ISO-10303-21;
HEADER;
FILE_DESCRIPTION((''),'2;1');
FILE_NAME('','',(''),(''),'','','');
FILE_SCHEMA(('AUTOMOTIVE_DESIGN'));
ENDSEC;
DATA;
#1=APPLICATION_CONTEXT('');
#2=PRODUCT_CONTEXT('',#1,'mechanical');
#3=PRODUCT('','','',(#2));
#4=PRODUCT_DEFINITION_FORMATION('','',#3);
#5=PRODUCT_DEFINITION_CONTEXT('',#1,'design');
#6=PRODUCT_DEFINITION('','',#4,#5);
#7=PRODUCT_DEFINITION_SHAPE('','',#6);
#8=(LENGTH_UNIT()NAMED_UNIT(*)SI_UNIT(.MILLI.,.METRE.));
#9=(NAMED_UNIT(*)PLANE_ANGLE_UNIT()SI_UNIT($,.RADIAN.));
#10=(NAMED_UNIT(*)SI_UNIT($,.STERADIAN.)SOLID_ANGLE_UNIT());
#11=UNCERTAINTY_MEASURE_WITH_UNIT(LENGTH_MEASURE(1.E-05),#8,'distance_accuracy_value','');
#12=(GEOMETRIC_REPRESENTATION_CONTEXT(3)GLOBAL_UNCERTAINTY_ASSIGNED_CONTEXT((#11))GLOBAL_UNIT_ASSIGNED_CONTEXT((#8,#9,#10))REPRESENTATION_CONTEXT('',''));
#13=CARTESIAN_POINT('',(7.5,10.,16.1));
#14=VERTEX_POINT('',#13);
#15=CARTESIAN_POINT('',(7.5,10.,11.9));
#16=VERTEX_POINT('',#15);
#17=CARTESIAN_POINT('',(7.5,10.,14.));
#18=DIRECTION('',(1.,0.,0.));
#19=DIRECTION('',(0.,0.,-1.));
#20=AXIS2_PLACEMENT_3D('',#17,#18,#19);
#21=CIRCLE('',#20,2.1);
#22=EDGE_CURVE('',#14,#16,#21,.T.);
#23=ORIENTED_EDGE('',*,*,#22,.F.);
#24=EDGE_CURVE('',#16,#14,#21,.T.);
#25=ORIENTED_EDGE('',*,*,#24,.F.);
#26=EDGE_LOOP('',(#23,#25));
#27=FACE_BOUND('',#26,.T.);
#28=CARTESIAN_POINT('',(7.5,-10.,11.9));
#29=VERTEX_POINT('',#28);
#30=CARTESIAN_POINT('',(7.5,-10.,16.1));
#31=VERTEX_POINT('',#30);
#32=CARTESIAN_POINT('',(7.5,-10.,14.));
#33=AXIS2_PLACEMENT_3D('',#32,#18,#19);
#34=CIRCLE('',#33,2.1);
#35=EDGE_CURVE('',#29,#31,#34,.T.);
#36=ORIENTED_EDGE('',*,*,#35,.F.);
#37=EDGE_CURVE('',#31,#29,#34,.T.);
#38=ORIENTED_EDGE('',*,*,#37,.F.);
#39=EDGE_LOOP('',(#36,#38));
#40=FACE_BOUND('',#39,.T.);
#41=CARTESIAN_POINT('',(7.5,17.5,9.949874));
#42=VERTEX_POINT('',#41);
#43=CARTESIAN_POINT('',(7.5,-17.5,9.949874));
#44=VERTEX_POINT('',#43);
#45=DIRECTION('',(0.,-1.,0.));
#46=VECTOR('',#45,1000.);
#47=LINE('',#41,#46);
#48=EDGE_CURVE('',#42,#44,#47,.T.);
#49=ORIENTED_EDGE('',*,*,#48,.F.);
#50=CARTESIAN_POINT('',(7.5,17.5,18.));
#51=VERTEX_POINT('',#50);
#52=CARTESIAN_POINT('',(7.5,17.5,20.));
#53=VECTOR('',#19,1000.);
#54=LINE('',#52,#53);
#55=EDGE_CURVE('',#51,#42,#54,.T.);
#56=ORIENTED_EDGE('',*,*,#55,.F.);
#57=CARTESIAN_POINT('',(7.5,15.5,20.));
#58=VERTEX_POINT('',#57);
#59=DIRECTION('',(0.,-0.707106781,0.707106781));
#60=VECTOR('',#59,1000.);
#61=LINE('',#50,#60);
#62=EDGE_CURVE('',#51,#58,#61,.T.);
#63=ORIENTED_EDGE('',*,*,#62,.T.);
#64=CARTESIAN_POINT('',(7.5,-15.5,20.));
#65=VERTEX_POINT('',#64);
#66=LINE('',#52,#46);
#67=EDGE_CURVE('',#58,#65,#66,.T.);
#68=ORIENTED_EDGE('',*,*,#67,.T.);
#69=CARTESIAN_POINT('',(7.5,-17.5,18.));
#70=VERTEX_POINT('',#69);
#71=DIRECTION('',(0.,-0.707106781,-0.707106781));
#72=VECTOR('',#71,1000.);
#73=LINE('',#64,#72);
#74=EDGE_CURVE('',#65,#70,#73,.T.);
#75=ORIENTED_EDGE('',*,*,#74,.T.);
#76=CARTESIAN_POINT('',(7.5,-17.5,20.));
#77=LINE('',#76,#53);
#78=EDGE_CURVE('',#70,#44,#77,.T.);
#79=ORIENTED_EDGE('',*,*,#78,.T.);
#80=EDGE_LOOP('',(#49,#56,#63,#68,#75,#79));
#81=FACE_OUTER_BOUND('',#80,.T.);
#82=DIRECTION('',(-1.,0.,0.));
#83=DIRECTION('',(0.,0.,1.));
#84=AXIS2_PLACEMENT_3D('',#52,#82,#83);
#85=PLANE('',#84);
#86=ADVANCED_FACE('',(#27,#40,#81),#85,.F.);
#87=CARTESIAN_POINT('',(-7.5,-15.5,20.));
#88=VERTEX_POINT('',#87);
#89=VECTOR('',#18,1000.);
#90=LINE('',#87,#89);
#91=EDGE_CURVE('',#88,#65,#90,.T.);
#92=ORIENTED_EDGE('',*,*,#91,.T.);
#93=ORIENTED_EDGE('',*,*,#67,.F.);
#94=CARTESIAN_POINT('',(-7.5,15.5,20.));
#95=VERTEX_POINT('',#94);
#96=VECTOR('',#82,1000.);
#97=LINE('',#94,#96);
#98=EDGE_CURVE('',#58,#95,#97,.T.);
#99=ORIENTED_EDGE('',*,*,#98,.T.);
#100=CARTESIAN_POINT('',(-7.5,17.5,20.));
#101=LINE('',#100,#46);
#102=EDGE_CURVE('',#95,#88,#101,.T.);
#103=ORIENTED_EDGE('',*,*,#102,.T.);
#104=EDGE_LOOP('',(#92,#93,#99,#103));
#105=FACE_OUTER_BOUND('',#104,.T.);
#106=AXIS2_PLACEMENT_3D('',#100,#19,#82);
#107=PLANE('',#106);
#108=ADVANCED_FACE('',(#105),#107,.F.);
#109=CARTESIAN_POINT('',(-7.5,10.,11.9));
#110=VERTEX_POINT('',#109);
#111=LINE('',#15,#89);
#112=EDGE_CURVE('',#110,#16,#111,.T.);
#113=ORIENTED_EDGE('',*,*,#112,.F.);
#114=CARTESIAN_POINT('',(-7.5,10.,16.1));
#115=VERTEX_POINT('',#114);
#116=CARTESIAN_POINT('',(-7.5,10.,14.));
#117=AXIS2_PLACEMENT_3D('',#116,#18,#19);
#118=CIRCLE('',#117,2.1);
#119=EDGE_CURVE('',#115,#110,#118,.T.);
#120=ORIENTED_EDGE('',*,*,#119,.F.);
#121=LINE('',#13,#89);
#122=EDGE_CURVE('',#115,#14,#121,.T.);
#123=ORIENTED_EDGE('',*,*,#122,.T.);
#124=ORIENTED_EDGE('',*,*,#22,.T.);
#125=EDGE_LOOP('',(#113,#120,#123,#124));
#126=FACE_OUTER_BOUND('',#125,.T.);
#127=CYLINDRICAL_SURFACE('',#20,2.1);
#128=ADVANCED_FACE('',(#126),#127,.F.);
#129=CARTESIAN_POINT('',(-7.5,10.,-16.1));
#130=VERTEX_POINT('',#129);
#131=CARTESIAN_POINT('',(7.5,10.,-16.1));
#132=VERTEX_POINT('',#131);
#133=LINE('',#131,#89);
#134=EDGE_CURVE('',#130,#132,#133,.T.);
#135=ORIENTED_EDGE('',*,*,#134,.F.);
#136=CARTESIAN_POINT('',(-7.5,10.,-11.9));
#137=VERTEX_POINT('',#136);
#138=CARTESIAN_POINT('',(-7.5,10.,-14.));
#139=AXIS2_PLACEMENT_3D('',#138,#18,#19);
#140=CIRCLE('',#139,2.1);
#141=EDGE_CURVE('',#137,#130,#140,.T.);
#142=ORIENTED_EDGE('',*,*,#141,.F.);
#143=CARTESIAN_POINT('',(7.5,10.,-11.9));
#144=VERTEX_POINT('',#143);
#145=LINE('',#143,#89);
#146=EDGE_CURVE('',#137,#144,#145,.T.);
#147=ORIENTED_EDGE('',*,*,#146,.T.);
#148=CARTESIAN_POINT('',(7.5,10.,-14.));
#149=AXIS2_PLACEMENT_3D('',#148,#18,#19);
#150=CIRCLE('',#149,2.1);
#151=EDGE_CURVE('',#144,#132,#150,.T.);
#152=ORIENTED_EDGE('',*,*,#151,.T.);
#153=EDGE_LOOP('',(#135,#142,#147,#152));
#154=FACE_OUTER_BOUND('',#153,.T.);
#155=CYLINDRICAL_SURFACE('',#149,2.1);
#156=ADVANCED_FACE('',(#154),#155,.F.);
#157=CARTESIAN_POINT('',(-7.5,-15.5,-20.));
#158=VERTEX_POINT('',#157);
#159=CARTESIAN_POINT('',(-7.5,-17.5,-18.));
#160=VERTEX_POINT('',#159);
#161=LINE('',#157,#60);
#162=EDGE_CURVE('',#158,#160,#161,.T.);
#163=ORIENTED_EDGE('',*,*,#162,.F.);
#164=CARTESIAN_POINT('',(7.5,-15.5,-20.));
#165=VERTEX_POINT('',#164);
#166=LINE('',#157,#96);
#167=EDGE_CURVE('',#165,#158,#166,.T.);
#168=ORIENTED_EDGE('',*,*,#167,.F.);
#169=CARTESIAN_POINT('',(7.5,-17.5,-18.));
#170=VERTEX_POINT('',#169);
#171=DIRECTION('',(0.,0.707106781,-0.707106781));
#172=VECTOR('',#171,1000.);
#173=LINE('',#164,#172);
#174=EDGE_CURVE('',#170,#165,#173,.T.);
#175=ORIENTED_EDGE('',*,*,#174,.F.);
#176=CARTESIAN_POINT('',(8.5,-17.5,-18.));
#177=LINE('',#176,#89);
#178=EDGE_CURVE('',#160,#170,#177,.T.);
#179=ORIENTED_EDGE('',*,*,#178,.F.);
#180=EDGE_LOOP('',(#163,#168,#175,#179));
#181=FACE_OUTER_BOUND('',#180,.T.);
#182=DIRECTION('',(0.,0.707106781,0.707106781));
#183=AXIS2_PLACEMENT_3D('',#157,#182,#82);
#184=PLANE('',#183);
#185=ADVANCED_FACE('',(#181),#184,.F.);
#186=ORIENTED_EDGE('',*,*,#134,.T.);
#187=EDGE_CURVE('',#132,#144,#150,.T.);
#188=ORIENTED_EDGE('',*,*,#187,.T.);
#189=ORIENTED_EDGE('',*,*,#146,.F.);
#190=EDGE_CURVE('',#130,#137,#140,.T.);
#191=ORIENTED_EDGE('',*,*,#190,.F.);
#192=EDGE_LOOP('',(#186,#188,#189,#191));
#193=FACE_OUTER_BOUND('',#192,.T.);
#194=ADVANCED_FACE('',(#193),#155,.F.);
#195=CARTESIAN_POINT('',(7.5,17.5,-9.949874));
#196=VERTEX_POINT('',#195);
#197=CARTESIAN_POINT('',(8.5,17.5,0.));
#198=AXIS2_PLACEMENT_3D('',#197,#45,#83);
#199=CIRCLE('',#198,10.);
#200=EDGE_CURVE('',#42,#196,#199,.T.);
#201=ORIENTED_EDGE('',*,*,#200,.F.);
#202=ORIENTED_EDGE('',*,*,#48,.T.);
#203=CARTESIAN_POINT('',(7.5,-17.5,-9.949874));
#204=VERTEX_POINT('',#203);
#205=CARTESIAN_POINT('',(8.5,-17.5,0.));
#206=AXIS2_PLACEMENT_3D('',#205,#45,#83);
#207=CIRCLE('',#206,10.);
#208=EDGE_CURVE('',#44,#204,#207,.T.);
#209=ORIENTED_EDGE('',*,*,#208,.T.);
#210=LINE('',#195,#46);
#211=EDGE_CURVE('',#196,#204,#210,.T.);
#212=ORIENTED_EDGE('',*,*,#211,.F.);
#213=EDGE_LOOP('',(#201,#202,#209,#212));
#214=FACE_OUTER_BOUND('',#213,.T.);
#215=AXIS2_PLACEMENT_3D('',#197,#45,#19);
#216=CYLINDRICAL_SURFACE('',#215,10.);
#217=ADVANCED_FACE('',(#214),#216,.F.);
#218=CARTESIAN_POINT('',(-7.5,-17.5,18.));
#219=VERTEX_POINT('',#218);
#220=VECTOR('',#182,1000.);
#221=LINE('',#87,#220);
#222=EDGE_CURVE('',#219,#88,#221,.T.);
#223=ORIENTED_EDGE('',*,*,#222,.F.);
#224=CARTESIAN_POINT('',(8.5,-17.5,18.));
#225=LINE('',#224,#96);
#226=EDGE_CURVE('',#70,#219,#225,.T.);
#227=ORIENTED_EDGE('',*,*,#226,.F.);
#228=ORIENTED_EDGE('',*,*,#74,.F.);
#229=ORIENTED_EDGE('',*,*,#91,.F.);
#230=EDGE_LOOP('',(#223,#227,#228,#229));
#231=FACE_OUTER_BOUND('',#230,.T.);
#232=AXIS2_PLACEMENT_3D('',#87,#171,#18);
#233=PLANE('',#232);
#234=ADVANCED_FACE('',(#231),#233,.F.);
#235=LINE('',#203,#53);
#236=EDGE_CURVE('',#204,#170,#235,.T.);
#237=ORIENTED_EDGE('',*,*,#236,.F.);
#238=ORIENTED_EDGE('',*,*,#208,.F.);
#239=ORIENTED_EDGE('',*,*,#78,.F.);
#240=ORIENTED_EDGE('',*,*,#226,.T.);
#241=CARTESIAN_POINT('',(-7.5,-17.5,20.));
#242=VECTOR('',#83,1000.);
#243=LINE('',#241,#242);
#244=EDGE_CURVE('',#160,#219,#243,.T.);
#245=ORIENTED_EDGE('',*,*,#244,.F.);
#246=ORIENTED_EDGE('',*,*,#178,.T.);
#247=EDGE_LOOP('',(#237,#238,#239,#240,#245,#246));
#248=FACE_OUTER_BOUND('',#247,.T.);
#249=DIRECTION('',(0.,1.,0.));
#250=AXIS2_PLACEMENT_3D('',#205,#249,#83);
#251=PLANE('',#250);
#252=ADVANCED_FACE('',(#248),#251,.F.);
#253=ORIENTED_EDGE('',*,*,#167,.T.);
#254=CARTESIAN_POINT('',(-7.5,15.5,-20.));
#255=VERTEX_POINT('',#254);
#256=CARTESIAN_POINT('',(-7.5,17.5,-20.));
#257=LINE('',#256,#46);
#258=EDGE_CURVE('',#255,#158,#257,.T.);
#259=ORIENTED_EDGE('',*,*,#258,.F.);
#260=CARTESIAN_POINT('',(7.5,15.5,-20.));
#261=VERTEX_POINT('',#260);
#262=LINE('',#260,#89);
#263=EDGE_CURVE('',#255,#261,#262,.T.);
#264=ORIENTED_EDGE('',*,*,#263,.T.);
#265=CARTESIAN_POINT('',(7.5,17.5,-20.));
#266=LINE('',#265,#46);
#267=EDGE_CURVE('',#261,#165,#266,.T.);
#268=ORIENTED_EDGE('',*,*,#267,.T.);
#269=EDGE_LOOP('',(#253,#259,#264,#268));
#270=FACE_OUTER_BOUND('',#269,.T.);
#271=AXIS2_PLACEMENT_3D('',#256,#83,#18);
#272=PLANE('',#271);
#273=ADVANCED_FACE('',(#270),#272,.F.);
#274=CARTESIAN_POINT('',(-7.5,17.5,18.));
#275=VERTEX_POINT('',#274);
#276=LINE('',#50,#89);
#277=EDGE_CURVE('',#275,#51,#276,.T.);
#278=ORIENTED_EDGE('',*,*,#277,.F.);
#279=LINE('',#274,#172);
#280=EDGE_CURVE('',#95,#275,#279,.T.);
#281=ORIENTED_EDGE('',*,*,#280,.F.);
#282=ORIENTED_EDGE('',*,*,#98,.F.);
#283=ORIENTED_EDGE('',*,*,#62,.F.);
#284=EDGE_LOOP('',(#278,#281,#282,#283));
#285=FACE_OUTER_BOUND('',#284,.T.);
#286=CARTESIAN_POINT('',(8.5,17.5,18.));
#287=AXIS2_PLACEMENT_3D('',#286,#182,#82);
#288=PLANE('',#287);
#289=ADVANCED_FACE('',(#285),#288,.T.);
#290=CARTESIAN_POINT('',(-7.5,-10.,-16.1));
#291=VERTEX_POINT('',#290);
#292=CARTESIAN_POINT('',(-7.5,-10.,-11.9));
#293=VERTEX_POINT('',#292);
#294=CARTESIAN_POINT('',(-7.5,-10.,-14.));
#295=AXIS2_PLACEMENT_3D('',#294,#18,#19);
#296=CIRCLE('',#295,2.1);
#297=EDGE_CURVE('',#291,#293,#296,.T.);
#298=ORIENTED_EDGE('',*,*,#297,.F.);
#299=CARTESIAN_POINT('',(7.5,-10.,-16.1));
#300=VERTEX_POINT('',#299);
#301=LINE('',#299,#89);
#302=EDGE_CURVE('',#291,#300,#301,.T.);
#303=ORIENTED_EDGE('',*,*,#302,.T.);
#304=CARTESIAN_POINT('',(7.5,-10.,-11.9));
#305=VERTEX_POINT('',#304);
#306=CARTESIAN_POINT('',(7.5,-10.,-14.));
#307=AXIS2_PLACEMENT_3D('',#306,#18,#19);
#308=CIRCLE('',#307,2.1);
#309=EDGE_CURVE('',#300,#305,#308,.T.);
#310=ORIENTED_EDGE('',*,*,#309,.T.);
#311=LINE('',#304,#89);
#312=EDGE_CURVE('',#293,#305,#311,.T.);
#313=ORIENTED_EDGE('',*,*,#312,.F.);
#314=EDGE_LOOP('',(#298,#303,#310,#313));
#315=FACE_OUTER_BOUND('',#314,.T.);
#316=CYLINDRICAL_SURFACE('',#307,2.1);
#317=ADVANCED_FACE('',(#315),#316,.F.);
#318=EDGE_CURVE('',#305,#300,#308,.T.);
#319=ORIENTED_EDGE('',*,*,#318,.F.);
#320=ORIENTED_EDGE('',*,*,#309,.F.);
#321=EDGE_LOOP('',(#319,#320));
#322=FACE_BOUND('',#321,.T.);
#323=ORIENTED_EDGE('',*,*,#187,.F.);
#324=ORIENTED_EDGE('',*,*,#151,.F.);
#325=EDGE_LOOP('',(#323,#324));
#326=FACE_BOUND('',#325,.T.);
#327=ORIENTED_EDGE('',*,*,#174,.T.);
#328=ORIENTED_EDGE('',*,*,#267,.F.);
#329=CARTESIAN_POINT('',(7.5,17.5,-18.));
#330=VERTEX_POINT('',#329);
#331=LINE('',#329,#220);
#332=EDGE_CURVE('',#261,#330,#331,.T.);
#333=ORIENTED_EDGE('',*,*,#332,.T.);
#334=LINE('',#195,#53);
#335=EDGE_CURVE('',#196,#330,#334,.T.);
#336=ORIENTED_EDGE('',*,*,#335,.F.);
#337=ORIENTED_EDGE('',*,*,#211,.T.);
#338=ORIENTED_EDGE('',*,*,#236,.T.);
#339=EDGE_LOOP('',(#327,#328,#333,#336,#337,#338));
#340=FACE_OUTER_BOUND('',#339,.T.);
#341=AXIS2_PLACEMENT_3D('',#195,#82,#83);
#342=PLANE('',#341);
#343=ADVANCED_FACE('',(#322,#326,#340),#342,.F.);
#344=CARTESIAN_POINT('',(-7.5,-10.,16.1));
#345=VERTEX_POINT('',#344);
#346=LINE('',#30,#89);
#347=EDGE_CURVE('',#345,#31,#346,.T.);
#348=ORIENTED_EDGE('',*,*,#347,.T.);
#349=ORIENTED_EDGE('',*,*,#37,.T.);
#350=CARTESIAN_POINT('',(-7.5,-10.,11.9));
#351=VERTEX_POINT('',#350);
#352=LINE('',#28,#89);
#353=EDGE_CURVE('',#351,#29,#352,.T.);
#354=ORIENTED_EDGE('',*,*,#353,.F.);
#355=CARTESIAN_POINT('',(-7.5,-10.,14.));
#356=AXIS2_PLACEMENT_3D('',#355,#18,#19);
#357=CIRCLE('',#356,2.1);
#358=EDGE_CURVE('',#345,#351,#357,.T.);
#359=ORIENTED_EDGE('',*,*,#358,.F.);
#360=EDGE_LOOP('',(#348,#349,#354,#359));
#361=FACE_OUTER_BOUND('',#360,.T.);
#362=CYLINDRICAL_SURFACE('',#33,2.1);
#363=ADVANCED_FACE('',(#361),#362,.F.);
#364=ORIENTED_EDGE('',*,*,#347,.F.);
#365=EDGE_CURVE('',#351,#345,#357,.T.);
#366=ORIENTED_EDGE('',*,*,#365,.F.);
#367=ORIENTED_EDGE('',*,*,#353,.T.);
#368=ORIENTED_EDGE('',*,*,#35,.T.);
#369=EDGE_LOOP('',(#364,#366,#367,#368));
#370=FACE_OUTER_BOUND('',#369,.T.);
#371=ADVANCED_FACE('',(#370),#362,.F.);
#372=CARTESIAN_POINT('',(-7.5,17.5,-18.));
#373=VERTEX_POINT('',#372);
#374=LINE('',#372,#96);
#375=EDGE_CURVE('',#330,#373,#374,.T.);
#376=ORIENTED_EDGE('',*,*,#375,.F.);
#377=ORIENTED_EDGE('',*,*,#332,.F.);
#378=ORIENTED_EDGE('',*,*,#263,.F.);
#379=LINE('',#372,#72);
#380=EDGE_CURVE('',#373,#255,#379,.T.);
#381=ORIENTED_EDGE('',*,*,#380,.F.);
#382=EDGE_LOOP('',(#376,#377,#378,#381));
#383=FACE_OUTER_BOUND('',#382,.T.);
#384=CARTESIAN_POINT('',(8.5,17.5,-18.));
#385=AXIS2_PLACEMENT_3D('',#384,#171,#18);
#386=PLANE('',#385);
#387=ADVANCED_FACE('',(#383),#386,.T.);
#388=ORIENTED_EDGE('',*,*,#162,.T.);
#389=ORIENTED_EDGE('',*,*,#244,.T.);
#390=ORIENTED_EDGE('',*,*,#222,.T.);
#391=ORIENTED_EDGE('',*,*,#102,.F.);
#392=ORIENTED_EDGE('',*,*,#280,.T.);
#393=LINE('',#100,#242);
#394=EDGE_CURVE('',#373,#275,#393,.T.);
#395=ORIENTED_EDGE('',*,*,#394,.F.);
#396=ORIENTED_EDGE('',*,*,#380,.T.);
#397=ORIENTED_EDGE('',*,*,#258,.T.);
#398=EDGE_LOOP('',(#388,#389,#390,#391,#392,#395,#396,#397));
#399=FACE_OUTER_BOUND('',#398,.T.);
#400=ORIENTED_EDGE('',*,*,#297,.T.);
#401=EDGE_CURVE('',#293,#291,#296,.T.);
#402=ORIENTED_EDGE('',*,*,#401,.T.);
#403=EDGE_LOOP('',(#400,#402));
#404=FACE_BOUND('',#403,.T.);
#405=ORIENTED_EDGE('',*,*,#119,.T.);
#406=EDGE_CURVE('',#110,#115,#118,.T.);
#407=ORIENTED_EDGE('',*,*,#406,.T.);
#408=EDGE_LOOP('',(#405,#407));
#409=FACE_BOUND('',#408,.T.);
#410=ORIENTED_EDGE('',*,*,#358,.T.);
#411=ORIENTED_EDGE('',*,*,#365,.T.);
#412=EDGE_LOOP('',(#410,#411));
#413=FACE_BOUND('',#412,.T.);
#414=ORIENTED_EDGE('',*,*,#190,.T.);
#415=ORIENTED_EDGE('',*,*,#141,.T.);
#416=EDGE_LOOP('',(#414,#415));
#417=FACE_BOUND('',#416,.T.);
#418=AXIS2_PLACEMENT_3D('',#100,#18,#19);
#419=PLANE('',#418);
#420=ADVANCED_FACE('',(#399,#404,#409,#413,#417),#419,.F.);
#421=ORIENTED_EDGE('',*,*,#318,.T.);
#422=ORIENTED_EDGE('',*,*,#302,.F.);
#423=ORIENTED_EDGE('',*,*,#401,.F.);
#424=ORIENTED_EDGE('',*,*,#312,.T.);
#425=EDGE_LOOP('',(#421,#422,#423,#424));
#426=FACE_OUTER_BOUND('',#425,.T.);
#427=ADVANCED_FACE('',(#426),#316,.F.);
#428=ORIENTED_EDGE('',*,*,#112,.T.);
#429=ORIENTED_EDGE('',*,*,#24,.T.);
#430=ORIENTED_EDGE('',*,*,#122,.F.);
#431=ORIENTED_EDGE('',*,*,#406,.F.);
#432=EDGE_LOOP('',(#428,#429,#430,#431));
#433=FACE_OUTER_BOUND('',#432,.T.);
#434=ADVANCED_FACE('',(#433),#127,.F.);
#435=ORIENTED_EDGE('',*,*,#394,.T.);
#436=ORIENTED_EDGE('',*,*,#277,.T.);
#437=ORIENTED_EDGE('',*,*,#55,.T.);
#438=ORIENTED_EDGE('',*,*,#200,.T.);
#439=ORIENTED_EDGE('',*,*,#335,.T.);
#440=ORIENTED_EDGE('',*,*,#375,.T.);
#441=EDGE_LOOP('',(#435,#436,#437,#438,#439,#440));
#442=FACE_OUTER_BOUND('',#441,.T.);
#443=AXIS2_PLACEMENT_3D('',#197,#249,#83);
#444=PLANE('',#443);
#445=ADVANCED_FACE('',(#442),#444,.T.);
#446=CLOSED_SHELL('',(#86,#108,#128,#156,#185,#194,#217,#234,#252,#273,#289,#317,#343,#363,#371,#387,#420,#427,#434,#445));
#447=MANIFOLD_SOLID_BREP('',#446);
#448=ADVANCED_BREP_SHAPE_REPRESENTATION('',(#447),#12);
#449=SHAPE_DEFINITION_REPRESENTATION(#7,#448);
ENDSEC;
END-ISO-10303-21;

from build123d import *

# Parameters (mm, degrees)
EXTRUDE_1_DEPTH    = 17.5
CHAMFER_1_SIZE     = 2
HOLE_WIZARD_M5_1_D = 4.2


with BuildPart() as part:
    # 草图1 → 凸台-拉伸1 (new, symmetric)
    with BuildSketch(Plane(origin=(0, 0, 0), x_dir=(1, 0, 0), z_dir=(0, 1, 0))):
        with BuildLine():
            Line((7.5, 9.949874371), (7.5, 20))
            Line((7.5, 20), (-7.5, 20))
            Line((-7.5, 20), (-7.5, -20))
            Line((-7.5, -20), (7.5, -20))
            Line((7.5, -20), (7.5, -9.949874371))
            ThreePointArc((7.5, -9.949874371), (-1.5, 0), (7.5, 9.949874371))
        make_face()
    extrude(amount=EXTRUDE_1_DEPTH, both=True)

    # 倒角1
    chamfer_1_edges = [part.edges().sort_by_distance(p)[0] for p in [
        (0, 17.5, 20),
        (0, 17.5, -20),
        (0, -17.5, 20),
        (0, -17.5, -20),
    ]]
    chamfer(chamfer_1_edges, length=CHAMFER_1_SIZE)

    # M5 螺纹孔1 (through all)
    with Locations(Plane(origin=(7.5, 0, 0), x_dir=(0, 0, -1), z_dir=(1, 0, 0))):
        with Locations((-14, 10), (14, 10), (14, -10), (-14, -10)):
            Hole(HOLE_WIZARD_M5_1_D / 2)


solid = part.part
